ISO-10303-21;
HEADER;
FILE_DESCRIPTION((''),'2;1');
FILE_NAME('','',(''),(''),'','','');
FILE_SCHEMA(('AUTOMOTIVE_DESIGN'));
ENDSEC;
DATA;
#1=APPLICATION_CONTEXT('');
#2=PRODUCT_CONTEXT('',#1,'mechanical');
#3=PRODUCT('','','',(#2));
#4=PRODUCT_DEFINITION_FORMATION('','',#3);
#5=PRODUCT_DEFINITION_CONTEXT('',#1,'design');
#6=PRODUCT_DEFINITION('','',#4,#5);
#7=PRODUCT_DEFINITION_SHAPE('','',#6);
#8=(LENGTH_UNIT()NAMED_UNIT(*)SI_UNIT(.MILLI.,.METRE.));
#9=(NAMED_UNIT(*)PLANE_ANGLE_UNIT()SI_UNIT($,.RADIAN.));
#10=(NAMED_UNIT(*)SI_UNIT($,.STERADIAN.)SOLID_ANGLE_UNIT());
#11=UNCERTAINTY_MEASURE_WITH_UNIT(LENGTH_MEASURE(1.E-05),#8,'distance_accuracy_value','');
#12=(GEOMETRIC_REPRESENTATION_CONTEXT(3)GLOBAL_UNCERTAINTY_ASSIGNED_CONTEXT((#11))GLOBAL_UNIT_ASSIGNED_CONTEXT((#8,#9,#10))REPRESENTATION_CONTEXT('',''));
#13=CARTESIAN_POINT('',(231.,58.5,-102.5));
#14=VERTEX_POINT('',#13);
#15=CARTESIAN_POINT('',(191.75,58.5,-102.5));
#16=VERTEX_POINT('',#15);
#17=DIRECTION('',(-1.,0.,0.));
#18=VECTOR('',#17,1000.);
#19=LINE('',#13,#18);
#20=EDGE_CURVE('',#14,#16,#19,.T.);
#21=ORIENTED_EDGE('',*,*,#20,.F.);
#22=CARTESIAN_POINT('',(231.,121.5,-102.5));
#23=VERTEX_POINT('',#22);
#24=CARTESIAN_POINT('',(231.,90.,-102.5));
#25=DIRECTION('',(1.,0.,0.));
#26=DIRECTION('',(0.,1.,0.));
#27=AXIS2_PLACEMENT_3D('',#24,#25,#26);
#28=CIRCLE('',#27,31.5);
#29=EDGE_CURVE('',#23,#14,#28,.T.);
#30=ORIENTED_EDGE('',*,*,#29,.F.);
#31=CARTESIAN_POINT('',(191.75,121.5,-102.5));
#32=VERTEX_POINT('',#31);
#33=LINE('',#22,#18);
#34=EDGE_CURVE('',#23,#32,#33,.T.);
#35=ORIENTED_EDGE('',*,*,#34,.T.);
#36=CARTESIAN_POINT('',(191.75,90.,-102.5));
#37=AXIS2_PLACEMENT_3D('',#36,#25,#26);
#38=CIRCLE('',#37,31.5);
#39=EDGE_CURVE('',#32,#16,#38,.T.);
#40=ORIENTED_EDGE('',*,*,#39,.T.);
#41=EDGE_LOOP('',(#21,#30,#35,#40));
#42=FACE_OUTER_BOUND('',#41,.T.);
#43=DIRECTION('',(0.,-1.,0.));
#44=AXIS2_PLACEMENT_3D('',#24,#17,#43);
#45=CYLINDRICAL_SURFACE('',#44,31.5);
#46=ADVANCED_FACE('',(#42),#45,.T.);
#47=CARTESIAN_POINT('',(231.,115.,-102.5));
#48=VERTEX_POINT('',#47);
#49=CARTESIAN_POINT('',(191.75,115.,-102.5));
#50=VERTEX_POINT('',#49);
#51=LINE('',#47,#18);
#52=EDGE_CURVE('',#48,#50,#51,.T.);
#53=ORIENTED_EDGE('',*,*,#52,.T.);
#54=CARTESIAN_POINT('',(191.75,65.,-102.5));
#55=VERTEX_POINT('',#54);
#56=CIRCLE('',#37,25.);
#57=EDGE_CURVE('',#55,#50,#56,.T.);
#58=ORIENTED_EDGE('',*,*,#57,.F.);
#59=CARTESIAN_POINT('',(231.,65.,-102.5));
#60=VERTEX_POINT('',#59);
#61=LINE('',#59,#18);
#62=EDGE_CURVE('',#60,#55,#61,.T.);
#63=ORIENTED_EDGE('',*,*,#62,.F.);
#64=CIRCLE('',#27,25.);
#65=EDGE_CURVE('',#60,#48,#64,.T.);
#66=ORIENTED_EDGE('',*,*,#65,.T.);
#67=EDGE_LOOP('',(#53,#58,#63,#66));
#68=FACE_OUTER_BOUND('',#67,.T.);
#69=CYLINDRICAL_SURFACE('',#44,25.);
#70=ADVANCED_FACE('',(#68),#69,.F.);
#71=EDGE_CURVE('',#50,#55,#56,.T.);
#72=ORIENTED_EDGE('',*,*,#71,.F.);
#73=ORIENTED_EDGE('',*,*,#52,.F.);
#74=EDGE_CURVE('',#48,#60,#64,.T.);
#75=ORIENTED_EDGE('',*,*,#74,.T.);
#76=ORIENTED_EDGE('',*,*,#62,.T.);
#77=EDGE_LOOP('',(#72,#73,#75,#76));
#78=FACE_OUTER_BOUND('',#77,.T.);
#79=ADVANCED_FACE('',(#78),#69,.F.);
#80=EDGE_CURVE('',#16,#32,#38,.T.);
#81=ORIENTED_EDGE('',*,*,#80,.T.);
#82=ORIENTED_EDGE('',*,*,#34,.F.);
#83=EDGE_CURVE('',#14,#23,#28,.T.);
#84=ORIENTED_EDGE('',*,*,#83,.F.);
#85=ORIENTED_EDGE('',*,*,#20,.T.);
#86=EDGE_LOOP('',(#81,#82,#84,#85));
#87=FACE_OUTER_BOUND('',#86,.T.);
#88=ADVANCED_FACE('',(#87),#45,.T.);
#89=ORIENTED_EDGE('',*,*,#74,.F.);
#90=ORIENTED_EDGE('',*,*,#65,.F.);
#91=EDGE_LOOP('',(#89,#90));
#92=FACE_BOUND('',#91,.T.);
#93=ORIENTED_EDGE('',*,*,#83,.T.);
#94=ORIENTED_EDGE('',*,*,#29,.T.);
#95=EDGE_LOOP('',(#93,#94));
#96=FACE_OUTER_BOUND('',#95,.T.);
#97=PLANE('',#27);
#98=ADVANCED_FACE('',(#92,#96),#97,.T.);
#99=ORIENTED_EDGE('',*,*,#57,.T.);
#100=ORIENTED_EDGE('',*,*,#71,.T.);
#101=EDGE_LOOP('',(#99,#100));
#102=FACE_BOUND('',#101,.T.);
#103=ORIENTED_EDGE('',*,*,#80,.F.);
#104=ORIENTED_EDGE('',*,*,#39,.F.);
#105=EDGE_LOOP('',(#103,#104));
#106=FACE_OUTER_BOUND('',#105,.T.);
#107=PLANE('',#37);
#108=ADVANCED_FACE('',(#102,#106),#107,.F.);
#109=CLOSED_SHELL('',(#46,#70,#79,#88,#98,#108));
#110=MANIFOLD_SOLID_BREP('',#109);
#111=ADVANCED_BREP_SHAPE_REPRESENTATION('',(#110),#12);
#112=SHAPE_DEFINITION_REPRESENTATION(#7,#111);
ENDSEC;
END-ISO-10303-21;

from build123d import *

# Parameters (mm, degrees)
SKETCH1_R           = 31.5
SKETCH1_R_2         = 25
BOSS_EXTRUDE1_DEPTH = 39.25


with BuildPart() as part:
    # Sketch1 → Boss-Extrude1 (new body)
    with BuildSketch(Plane(origin=(191.75, 0, 0), x_dir=(0, 0, -1), z_dir=(1, 0, 0))):
        with Locations(Location((102.5, 90, 0), (0, 0, 90))):
            Circle(SKETCH1_R)
        with Locations(Location((102.5, 90, 0), (0, 0, 90))):
            Circle(SKETCH1_R_2, mode=Mode.SUBTRACT)
    extrude(amount=BOSS_EXTRUDE1_DEPTH)


solid = part.part
